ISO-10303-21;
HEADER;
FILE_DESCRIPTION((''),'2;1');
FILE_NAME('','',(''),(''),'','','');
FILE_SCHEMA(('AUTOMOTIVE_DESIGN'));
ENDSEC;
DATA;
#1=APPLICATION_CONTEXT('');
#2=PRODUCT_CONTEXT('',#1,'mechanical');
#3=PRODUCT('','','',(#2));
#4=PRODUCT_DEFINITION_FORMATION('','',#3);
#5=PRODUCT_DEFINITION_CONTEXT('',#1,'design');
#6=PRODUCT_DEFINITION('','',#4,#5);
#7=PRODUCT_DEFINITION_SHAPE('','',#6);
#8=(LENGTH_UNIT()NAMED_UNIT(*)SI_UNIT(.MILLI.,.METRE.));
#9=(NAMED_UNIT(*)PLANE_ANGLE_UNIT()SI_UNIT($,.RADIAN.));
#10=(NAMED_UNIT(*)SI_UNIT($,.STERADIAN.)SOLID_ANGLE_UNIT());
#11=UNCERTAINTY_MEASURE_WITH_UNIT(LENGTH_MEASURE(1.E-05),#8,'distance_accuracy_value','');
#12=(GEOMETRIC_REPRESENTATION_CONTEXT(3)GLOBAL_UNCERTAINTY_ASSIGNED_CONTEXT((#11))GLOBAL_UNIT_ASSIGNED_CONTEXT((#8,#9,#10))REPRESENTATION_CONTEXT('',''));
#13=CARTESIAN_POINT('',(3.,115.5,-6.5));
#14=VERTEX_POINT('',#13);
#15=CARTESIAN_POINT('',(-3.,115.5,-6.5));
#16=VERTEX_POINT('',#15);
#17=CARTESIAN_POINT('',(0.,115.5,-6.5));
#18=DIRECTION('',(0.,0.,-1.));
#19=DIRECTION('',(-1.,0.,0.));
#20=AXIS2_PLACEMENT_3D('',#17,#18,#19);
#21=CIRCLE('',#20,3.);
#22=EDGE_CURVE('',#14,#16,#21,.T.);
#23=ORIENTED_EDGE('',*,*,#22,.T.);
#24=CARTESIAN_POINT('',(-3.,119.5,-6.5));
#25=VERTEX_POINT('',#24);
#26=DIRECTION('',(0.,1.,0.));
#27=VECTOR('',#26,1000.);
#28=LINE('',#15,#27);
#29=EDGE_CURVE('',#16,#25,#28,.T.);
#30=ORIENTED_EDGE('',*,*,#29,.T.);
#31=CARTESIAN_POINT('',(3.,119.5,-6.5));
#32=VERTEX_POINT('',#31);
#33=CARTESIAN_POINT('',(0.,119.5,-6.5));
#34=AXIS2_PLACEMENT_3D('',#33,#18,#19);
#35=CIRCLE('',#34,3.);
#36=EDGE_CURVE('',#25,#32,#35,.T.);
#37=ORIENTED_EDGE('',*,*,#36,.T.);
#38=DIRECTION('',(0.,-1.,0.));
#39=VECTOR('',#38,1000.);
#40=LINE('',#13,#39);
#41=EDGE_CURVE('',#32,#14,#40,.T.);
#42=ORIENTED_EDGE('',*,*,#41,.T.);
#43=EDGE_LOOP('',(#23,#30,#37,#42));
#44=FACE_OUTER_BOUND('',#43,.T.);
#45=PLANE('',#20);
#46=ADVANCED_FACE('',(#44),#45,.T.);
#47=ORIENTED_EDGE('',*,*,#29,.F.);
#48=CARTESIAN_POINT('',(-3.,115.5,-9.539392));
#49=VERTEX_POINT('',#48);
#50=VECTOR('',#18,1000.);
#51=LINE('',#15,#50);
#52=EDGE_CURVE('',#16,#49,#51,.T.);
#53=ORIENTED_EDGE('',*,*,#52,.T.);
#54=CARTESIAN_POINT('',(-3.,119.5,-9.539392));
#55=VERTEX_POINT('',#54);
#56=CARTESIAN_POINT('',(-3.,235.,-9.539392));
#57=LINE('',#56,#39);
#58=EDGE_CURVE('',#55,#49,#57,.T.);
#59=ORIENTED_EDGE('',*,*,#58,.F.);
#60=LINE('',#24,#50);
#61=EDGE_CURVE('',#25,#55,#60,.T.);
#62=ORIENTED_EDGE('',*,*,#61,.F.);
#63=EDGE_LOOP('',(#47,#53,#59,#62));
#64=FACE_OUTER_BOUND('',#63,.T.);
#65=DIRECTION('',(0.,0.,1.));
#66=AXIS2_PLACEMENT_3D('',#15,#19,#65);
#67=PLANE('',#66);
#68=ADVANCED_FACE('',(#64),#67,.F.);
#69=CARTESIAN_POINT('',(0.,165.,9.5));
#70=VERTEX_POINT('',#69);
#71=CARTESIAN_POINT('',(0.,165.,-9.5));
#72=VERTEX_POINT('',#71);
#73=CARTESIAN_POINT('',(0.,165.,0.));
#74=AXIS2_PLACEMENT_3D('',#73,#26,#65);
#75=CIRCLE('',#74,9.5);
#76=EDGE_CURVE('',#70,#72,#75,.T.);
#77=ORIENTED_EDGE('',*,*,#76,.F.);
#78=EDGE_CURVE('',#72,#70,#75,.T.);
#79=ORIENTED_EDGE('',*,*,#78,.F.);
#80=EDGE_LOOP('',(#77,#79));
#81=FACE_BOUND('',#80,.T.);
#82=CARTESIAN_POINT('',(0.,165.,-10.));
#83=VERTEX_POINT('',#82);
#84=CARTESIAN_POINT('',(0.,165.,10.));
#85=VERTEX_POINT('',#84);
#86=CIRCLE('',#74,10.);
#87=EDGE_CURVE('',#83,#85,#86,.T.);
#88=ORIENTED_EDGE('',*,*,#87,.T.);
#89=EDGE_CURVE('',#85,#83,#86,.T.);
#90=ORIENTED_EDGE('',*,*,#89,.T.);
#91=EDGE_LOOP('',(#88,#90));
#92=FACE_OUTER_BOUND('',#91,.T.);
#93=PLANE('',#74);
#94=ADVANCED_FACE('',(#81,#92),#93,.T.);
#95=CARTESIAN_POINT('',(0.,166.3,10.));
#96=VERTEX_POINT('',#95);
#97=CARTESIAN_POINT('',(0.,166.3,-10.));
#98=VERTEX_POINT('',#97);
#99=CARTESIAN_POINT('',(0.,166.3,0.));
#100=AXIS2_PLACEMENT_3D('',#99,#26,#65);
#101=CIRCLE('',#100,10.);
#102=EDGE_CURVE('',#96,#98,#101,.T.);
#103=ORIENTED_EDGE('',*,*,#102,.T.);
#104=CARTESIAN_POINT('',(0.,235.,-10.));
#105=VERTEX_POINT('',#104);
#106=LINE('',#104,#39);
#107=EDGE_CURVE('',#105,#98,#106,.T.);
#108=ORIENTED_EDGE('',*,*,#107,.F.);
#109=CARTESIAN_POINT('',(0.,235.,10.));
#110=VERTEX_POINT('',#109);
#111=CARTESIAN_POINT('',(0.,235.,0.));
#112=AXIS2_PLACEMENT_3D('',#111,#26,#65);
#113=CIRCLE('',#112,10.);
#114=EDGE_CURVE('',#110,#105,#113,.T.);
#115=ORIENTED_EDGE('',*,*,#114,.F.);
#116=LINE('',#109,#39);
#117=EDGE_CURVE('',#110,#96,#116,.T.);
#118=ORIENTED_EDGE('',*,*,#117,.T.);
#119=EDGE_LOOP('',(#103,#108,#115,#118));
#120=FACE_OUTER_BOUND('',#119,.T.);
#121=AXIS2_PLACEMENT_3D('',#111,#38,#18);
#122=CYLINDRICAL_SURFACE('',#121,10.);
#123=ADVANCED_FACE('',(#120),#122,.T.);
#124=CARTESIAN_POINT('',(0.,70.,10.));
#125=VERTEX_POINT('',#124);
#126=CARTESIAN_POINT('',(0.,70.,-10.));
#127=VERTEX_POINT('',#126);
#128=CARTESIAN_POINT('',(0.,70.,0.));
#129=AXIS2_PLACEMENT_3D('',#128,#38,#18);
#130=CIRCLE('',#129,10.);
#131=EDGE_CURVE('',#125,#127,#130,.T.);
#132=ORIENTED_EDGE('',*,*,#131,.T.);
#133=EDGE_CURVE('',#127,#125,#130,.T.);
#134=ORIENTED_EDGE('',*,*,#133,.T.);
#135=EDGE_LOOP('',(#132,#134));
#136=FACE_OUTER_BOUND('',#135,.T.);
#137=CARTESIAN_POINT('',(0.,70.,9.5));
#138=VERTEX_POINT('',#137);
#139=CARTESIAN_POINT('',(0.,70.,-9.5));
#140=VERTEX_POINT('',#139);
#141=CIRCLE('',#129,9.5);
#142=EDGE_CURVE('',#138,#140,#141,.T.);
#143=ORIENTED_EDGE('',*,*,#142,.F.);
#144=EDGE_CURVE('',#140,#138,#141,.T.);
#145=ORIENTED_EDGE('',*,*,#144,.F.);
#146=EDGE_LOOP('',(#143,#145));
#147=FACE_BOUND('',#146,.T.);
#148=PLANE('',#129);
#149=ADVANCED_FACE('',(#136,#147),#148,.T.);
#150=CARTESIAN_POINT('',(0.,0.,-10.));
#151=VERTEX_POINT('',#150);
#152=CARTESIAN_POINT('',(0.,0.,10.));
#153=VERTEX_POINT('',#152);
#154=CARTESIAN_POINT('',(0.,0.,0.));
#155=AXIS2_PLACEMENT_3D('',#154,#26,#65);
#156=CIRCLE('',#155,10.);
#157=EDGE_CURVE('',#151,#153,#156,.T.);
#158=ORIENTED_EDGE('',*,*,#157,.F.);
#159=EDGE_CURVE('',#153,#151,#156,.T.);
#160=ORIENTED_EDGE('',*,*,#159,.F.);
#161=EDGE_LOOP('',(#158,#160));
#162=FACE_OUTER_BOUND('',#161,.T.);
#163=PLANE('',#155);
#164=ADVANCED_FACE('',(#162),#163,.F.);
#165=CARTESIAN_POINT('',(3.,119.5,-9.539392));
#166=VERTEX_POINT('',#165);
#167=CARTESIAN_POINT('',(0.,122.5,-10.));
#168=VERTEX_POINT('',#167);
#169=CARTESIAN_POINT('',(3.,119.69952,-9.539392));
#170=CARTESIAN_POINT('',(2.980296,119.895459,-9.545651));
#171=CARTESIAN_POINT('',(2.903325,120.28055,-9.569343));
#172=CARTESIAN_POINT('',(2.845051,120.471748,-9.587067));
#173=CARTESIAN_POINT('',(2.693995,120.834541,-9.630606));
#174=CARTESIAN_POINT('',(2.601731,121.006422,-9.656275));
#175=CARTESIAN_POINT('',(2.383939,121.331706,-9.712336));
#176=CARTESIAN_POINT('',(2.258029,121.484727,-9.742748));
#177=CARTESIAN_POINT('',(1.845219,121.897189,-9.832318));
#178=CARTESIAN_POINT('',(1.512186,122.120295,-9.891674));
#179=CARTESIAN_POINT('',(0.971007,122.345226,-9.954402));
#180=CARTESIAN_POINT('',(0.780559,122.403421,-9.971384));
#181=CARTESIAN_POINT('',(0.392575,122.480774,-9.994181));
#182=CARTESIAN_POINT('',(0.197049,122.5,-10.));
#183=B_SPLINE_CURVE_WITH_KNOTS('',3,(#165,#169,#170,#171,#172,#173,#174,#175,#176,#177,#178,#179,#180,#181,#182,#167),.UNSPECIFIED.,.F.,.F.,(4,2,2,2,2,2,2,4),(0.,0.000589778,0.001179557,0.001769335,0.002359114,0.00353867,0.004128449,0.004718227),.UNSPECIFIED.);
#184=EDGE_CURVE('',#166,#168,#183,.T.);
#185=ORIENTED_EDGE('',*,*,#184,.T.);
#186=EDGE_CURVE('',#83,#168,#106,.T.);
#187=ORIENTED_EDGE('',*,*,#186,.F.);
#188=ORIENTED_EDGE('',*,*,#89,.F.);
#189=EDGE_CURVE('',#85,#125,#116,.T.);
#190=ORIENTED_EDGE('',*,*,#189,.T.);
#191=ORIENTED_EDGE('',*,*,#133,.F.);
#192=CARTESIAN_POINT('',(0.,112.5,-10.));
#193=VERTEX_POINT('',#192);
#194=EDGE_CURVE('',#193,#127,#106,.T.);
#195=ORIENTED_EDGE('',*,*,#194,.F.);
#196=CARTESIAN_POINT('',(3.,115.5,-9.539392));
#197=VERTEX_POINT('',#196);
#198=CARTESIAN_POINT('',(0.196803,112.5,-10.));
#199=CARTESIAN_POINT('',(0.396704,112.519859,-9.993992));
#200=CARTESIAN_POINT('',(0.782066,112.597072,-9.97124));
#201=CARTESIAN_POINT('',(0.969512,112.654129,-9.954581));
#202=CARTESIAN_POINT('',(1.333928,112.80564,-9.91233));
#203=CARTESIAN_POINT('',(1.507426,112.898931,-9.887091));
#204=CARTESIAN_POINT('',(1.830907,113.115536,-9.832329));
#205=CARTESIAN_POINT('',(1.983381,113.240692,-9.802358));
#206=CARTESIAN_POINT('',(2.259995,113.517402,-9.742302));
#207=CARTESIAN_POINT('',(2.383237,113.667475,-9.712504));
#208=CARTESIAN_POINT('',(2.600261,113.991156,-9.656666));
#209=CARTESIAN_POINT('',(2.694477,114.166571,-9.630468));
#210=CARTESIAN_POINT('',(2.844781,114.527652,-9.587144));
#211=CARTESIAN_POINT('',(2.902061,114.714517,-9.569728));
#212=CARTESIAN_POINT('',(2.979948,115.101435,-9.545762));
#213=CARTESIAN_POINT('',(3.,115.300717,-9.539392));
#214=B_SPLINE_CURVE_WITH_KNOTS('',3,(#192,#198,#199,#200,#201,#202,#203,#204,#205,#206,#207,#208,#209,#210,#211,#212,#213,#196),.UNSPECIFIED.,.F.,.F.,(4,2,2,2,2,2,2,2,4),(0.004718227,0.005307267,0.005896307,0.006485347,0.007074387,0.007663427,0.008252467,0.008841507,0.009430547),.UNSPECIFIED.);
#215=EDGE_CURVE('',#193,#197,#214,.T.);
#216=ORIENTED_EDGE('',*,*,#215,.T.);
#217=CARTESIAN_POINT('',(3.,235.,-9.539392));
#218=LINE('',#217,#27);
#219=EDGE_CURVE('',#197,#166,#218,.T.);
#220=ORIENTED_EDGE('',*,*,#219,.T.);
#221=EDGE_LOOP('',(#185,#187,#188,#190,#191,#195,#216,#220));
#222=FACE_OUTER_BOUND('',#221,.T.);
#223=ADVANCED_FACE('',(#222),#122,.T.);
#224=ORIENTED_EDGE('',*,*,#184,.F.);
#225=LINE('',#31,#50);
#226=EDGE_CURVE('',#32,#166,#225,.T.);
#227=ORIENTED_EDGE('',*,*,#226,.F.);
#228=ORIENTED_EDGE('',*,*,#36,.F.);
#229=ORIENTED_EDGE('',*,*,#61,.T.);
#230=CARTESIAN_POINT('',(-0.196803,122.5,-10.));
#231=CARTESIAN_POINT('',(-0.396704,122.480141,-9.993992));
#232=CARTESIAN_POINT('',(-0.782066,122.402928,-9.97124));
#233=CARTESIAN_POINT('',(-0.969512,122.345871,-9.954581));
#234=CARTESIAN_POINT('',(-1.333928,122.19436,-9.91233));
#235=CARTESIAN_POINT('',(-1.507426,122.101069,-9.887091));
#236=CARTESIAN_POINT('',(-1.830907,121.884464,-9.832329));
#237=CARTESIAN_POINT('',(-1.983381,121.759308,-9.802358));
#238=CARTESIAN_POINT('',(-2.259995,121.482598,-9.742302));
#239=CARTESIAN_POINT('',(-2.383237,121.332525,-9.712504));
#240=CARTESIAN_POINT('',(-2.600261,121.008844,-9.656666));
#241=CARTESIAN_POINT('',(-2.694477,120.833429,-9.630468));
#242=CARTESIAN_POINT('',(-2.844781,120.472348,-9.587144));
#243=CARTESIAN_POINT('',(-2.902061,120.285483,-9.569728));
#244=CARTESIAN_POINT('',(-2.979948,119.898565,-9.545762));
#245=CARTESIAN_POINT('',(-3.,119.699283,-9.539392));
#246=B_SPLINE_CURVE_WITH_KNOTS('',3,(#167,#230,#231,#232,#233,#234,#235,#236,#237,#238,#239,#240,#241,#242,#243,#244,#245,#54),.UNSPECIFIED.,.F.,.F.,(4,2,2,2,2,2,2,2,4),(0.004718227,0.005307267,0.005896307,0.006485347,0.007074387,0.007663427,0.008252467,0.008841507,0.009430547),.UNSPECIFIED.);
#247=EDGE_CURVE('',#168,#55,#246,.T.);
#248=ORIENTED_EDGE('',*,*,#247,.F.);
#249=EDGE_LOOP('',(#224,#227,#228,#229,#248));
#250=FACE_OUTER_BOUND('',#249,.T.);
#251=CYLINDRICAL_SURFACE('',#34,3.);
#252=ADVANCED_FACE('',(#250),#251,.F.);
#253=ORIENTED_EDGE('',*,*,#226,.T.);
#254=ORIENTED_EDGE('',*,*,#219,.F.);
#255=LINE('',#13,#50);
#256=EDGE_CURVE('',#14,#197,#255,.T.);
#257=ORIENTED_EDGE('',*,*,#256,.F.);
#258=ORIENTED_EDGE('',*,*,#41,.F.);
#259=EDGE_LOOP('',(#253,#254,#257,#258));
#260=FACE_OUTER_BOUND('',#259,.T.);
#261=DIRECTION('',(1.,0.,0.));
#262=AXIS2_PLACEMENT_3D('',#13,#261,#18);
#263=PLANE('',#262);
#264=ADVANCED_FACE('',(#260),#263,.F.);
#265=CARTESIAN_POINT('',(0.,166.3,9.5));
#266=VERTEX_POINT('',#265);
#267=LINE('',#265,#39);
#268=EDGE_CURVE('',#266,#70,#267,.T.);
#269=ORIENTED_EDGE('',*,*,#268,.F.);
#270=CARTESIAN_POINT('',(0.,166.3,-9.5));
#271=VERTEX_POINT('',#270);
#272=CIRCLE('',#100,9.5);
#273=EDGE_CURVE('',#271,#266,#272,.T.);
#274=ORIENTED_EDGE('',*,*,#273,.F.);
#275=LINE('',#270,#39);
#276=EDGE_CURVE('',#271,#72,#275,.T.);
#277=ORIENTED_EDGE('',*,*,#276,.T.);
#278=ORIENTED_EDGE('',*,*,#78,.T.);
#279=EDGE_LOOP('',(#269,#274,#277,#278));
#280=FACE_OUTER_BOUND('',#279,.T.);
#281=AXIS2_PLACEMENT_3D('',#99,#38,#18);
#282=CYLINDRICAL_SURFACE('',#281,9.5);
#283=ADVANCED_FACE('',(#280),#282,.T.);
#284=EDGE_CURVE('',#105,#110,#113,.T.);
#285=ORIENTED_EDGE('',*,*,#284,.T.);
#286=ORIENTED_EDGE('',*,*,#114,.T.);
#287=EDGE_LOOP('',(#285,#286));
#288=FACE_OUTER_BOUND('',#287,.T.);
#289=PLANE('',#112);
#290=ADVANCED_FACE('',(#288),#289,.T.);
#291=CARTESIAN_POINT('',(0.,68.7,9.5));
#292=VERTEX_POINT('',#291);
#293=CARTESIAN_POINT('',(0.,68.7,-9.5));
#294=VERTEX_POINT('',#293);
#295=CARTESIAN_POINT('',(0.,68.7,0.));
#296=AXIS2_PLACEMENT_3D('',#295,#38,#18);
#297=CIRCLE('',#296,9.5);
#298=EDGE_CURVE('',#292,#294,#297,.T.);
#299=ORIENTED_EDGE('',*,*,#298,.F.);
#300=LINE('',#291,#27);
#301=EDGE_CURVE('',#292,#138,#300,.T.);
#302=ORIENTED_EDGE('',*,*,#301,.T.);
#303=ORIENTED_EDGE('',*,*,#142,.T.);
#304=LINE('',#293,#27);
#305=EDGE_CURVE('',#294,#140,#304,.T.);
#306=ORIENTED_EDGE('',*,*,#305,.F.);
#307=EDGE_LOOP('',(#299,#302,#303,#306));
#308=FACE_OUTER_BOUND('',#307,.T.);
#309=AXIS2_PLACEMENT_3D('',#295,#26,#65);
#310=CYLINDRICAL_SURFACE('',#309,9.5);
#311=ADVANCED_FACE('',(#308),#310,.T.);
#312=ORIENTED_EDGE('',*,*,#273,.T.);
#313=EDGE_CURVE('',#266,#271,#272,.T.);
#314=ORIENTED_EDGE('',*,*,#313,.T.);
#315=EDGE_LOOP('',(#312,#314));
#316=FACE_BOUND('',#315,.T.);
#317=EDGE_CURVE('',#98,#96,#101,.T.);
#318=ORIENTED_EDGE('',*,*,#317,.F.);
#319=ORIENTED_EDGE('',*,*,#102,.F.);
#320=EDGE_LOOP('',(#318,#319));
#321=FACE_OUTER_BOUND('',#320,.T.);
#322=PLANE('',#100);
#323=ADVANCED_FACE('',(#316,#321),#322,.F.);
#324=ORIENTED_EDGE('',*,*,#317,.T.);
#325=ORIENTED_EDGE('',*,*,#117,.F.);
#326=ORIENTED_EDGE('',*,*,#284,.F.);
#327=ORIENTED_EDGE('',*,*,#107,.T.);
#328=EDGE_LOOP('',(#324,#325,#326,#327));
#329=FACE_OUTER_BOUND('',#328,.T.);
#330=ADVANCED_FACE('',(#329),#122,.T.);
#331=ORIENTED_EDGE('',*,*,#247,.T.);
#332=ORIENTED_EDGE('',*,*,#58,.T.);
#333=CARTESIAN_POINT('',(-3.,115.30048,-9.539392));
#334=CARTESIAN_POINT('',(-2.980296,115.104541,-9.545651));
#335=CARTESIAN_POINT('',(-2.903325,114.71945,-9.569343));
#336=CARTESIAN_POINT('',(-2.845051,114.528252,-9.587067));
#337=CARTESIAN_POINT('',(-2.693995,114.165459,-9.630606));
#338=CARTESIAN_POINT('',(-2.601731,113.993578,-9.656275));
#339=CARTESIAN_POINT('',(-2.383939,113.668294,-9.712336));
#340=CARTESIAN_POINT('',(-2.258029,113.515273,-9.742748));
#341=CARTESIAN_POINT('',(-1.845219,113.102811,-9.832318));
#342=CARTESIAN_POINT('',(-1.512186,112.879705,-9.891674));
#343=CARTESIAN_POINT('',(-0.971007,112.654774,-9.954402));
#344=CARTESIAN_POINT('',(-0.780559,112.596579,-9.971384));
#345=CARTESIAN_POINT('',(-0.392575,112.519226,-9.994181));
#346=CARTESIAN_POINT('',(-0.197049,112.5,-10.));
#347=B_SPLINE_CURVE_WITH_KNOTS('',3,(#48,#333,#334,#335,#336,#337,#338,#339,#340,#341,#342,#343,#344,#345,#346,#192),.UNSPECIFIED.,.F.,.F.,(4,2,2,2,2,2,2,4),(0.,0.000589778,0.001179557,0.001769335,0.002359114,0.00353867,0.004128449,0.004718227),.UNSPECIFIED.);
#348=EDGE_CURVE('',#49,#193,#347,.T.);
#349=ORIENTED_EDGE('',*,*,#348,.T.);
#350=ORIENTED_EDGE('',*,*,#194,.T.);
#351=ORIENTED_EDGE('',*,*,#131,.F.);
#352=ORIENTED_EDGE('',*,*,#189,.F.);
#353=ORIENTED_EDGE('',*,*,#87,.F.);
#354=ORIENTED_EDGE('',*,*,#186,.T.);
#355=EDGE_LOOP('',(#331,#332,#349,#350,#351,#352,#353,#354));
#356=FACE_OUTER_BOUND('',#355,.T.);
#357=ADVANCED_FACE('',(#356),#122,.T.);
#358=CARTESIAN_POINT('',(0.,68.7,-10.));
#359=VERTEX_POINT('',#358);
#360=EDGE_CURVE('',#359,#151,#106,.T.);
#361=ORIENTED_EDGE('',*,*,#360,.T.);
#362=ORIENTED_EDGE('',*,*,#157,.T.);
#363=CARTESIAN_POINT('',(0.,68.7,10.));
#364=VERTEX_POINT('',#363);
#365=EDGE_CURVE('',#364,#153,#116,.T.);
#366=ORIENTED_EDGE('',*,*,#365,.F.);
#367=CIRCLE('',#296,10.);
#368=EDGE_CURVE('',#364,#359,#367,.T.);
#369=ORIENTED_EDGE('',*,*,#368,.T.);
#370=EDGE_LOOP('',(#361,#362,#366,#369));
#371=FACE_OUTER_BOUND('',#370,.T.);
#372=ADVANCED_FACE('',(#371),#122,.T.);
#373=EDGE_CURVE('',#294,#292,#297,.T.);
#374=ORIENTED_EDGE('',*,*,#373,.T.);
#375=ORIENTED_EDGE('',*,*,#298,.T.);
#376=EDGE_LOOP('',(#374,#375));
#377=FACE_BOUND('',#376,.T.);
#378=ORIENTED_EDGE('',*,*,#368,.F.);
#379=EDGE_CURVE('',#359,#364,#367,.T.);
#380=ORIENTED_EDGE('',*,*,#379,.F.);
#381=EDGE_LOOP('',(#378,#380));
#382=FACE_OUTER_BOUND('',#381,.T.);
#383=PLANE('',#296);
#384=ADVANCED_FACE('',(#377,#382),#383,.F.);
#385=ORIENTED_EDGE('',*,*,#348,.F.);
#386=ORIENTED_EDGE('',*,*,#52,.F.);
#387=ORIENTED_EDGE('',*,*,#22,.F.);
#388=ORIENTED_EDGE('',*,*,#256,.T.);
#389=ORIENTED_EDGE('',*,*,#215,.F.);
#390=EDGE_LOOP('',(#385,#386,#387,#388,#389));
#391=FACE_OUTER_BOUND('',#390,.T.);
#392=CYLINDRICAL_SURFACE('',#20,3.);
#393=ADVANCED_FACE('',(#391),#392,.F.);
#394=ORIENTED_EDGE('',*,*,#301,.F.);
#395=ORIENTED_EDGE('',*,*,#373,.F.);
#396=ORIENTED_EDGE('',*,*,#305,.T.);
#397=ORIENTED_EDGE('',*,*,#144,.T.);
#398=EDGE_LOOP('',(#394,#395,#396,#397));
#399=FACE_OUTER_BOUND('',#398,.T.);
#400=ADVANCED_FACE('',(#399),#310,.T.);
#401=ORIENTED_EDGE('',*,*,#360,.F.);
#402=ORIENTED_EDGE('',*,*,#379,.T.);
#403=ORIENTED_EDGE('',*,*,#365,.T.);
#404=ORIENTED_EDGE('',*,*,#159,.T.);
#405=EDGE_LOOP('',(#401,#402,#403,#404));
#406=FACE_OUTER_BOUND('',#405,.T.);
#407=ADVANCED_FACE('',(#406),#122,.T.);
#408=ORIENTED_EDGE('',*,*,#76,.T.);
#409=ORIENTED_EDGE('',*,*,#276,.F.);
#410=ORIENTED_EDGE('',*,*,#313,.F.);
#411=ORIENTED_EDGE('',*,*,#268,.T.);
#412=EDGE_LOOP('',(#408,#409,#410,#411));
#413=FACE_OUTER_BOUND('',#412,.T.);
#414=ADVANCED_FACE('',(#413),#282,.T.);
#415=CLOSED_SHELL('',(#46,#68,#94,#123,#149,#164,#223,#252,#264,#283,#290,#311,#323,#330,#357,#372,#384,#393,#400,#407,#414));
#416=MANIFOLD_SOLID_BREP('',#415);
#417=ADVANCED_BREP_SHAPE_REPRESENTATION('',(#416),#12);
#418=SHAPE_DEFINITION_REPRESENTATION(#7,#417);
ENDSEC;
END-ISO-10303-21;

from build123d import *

# Parameters (mm, degrees)
SKETCH_1_R          = 10
EXTRUDE_1_DEPTH     = 235
CUT_EXTRUDE_START   = 1.3
SKETCH_7_R          = 10
SKETCH_7_R_2        = 9.5
CUT_EXTRUDE_3_DEPTH = 1.3
SKETCH_8_R          = 10
SKETCH_8_R_2        = 9.5
CUT_EXTRUDE_4_DEPTH = 1.3
ZJCQC_DEPTH         = 3.5


with BuildPart() as part:
    # 草图1 → 凸台-拉伸1 (new body)
    with BuildSketch(Plane(origin=(0, 0, 0), x_dir=(1, 0, 0), z_dir=(0, 1, 0))):
        with Locations(Location((0, 0, 0), (0, 0, 90))):
            Circle(SKETCH_1_R)
    extrude(amount=EXTRUDE_1_DEPTH)

    # 草图7 → 切除-拉伸3 (cut)
    with BuildSketch(Plane(origin=(0, 70, 0), x_dir=(-1, 0, 0), z_dir=(0, -1, 0)).offset(CUT_EXTRUDE_START)):
        with Locations(Location((0, 0, 0), (0, 0, 90))):
            Circle(SKETCH_7_R)
        with Locations(Location((0, 0, 0), (0, 0, 90))):
            Circle(SKETCH_7_R_2, mode=Mode.SUBTRACT)
    extrude(amount=-CUT_EXTRUDE_3_DEPTH, mode=Mode.SUBTRACT)

    # 草图8 → 切除-拉伸4 (cut)
    with BuildSketch(Plane(origin=(0, 165, 0), x_dir=(1, 0, 0), z_dir=(0, 1, 0))):
        with Locations(Location((0, 0, 0), (0, 0, 90))):
            Circle(SKETCH_8_R)
        with Locations(Location((0, 0, 0), (0, 0, 90))):
            Circle(SKETCH_8_R_2, mode=Mode.SUBTRACT)
    extrude(amount=CUT_EXTRUDE_4_DEPTH, mode=Mode.SUBTRACT)

    # MyToolsZJC → ZJCQC (cut)
    with BuildSketch(Plane.YX.offset(10)):
        with BuildLine():
            Line((115.5, 3), (119.5, 3))
            ThreePointArc((119.5, 3), (122.5, 0), (119.5, -3))
            Line((119.5, -3), (115.5, -3))
            ThreePointArc((115.5, -3), (112.5, 0), (115.5, 3))
        make_face()
    extrude(amount=-ZJCQC_DEPTH, mode=Mode.SUBTRACT)


solid = part.part
